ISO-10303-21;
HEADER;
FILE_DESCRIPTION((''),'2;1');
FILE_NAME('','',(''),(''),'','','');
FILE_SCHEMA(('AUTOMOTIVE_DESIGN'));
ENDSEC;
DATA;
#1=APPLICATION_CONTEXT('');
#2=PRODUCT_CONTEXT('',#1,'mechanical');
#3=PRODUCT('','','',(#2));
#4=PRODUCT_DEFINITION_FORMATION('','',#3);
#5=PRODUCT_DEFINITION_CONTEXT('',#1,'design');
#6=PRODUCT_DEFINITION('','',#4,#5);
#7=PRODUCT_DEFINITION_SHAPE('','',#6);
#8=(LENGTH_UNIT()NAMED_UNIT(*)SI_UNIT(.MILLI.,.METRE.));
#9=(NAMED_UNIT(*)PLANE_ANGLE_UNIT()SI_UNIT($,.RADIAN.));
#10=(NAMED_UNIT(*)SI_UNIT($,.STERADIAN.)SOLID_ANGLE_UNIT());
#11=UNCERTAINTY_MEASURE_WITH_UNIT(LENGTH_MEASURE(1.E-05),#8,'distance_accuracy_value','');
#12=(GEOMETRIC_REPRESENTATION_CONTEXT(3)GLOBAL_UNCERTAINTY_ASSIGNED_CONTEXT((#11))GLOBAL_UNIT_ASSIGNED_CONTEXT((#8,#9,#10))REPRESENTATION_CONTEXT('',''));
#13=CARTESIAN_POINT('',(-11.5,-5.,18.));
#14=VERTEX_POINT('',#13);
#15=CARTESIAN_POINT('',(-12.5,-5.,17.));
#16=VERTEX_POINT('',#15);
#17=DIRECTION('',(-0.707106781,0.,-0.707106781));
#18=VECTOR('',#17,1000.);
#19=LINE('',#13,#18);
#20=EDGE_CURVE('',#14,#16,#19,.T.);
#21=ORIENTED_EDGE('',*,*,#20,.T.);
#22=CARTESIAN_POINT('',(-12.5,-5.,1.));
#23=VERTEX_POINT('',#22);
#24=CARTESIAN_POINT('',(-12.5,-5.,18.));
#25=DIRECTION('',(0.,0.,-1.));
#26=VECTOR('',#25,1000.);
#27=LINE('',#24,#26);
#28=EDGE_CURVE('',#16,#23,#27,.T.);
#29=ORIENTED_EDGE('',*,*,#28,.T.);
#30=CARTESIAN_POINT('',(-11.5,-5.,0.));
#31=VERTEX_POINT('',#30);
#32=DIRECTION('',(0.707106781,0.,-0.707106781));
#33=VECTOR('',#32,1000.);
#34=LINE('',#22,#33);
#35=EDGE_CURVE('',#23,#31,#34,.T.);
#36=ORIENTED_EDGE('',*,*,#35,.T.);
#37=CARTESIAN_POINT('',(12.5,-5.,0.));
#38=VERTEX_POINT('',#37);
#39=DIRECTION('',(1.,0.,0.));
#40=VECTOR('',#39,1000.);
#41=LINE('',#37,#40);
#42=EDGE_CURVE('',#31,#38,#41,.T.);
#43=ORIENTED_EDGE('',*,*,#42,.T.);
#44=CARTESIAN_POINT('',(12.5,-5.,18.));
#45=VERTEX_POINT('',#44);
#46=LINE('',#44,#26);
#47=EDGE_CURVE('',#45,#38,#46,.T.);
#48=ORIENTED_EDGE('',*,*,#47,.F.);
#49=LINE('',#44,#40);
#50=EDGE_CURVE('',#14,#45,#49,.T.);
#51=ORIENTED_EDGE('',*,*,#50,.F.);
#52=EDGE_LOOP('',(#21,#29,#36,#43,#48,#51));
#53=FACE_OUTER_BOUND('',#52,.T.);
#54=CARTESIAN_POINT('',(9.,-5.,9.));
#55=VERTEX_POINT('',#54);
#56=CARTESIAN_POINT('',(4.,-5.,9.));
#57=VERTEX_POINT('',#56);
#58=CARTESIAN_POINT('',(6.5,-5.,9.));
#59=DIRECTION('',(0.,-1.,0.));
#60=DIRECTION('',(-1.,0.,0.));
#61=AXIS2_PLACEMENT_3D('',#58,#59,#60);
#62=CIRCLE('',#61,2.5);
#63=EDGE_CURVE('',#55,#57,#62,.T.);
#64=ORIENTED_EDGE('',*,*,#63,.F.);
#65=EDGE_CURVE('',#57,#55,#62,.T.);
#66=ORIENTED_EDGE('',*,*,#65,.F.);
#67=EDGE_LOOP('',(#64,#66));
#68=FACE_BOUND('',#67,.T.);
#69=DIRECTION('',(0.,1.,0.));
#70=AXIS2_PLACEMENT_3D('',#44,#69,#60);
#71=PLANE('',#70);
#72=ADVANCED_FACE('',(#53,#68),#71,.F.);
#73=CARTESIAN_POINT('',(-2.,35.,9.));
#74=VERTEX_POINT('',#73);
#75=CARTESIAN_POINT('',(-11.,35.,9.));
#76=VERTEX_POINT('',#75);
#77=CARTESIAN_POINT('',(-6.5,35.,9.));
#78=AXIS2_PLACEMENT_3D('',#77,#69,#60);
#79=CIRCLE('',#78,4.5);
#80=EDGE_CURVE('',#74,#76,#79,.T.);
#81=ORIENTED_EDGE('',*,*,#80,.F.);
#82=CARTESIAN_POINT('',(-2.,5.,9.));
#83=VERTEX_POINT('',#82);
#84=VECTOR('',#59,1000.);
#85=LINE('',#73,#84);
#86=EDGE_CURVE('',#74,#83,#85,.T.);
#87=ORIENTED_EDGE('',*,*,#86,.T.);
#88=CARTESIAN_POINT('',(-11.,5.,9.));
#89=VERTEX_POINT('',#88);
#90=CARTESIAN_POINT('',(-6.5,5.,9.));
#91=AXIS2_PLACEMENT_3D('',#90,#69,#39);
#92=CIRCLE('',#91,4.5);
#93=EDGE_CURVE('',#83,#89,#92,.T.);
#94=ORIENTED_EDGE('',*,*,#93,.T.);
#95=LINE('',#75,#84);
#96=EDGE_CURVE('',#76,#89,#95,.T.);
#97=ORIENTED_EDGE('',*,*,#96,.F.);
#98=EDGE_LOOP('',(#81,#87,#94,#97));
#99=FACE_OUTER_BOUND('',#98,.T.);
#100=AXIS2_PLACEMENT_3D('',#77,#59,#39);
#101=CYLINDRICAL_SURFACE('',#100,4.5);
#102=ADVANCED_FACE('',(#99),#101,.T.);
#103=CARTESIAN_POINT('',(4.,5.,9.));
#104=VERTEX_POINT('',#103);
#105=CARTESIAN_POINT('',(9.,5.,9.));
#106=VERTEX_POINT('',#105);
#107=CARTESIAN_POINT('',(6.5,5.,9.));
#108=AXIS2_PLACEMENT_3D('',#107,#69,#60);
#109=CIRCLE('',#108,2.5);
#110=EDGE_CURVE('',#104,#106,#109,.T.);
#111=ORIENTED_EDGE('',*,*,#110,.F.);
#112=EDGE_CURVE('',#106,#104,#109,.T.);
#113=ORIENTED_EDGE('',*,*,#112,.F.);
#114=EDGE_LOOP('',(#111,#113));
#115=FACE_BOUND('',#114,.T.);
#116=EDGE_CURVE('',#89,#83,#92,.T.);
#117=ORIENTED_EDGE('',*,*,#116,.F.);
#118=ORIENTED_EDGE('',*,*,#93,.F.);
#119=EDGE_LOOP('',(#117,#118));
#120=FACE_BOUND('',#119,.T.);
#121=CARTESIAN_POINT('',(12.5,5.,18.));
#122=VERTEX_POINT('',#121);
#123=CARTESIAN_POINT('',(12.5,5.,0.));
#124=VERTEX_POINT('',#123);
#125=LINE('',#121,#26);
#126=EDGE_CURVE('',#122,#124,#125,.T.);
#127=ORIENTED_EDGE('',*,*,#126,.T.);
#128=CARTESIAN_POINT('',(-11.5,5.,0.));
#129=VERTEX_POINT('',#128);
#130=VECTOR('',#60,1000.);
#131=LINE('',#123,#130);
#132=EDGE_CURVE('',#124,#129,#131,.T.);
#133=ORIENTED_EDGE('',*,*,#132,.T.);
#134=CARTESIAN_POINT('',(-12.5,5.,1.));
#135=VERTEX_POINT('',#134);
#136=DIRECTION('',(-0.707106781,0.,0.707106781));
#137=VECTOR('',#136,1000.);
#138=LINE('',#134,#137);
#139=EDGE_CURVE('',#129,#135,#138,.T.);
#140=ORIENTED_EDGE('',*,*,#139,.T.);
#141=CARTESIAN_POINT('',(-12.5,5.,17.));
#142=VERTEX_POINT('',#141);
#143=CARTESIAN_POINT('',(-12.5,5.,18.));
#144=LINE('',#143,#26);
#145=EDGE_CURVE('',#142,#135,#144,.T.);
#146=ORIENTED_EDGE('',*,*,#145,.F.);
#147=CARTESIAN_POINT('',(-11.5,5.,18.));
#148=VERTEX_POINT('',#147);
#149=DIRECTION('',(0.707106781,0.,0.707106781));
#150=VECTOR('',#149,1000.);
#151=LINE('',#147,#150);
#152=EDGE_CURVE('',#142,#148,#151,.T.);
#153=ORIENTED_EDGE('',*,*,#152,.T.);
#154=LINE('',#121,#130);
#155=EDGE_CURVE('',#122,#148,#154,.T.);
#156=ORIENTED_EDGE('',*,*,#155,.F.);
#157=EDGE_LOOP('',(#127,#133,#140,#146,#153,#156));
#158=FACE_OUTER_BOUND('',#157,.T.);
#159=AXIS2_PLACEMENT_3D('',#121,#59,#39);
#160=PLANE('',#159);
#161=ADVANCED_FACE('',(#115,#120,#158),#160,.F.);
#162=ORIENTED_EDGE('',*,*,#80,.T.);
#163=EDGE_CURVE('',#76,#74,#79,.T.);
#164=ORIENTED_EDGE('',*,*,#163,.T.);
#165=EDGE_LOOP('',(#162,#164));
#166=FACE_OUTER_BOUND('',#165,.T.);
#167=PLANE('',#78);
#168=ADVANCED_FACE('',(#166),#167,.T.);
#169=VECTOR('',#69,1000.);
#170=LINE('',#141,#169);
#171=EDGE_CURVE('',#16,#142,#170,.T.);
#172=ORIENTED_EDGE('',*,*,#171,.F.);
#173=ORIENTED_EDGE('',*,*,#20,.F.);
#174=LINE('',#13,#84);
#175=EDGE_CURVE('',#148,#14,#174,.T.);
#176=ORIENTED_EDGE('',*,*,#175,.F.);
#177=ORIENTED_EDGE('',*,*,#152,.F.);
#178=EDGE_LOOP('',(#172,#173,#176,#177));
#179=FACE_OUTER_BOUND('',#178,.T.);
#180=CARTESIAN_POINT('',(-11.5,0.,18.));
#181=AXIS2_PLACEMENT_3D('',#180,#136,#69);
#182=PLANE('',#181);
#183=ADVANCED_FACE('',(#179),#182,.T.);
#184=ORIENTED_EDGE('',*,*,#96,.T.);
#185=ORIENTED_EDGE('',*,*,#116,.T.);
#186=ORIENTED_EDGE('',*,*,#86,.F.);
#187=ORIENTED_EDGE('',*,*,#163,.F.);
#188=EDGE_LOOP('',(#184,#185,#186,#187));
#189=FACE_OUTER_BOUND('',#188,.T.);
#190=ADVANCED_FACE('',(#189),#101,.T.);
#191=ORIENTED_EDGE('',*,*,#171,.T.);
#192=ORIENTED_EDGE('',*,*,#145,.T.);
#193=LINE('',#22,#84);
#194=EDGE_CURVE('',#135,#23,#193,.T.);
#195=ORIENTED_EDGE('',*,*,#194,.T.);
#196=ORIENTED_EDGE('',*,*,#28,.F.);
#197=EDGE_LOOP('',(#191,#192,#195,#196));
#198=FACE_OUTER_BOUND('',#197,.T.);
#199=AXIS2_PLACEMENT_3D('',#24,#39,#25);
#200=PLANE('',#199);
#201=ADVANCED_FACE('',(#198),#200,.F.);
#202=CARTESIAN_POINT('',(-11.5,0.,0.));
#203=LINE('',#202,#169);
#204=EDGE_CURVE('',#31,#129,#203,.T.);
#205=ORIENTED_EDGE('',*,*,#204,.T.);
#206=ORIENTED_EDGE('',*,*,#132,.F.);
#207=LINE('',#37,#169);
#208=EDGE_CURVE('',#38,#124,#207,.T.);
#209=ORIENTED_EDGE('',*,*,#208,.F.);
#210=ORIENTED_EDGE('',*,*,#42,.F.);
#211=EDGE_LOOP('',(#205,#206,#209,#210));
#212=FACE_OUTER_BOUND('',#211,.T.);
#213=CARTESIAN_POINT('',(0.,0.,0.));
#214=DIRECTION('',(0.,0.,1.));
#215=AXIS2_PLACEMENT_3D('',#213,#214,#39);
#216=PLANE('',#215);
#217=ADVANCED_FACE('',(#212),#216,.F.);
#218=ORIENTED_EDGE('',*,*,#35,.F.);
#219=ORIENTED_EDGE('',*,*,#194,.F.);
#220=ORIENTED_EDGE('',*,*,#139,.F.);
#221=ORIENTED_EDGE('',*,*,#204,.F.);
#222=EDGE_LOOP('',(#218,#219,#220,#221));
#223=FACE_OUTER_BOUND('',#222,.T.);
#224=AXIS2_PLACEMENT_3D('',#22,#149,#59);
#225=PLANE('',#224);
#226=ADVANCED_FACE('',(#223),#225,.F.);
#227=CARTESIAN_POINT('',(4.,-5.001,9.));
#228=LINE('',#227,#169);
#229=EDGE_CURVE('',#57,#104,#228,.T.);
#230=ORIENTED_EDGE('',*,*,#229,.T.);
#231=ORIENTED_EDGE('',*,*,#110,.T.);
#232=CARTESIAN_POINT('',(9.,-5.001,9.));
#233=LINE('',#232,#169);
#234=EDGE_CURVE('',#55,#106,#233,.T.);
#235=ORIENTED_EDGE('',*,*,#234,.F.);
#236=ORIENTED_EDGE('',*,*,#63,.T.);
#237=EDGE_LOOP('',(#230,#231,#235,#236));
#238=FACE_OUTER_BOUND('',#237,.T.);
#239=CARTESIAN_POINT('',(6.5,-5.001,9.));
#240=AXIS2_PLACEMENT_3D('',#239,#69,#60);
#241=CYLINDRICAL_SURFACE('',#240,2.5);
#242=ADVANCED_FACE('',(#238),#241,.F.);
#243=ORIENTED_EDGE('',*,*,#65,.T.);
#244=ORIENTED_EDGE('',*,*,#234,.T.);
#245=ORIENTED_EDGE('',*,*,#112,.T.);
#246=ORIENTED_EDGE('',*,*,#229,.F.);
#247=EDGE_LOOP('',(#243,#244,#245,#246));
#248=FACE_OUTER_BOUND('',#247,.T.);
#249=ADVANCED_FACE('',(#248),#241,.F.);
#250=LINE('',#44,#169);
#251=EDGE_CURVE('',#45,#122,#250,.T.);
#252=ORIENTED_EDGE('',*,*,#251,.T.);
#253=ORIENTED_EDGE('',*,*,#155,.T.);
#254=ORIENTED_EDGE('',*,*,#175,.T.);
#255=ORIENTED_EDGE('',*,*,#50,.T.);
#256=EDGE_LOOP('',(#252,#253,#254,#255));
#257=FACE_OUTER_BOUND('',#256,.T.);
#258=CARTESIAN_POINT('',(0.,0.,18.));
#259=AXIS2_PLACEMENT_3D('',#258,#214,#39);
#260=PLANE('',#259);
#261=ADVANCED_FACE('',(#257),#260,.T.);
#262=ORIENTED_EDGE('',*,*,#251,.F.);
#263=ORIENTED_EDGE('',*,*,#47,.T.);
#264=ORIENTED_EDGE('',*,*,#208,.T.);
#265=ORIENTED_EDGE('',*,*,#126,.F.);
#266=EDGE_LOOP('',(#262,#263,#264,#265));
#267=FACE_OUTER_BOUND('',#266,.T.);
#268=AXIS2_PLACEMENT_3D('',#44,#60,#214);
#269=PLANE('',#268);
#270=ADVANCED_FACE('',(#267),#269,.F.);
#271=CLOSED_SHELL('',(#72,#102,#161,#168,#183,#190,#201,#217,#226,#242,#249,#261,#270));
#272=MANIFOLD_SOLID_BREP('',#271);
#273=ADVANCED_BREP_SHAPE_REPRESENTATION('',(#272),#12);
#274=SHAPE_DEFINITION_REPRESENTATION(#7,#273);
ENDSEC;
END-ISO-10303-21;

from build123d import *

# Parameters (mm, degrees)
SKETCH_1_W          = 25
SKETCH_1_H          = 10
EXTRUDE_1_DEPTH     = 18
SKETCH_2_R          = 4.5
EXTRUDE_2_DEPTH     = 30
CUT_EXTRUDE_1_REACH = 39.152
SKETCH_3_R          = 2.5
CHAMFER_1_SIZE      = 1


with BuildPart() as part:
    # 草图1 → 凸台-拉伸1 (new body)
    with BuildSketch(Plane.XY):
        Rectangle(SKETCH_1_W, SKETCH_1_H)
    extrude(amount=EXTRUDE_1_DEPTH)

    # 草图2 → 凸台-拉伸2 (add)
    with BuildSketch(Plane(origin=(0, 5, 0), x_dir=(1, 0, 0), z_dir=(0, 1, 0))):
        with Locations((-6.5, -9)):
            Circle(SKETCH_2_R)
    extrude(amount=EXTRUDE_2_DEPTH)

    # 草图3 → 切除-拉伸1 (cut, up to next)
    with BuildSketch(Plane(origin=(0, 5, 0), x_dir=(1, 0, 0), z_dir=(0, 1, 0)), mode=Mode.PRIVATE) as cut_extrude_1_sk1:
        with Locations(Location((6.5, -9, 0), (0, 0, 180))):
            Circle(SKETCH_3_R)
    cut_extrude_1_tool1 = extrude(cut_extrude_1_sk1.sketch, amount=-CUT_EXTRUDE_1_REACH, mode=Mode.PRIVATE) & part.part
    add(cut_extrude_1_tool1.solids().sort_by_distance((6.5, 5, 9))[0], mode=Mode.SUBTRACT)

    # 倒角1
    chamfer_1_edges = [part.edges().sort_by_distance(p)[0] for p in [
        (-12.5, 0, 18),
        (-12.5, 0, 0),
    ]]
    chamfer(chamfer_1_edges, length=CHAMFER_1_SIZE)


solid = part.part
